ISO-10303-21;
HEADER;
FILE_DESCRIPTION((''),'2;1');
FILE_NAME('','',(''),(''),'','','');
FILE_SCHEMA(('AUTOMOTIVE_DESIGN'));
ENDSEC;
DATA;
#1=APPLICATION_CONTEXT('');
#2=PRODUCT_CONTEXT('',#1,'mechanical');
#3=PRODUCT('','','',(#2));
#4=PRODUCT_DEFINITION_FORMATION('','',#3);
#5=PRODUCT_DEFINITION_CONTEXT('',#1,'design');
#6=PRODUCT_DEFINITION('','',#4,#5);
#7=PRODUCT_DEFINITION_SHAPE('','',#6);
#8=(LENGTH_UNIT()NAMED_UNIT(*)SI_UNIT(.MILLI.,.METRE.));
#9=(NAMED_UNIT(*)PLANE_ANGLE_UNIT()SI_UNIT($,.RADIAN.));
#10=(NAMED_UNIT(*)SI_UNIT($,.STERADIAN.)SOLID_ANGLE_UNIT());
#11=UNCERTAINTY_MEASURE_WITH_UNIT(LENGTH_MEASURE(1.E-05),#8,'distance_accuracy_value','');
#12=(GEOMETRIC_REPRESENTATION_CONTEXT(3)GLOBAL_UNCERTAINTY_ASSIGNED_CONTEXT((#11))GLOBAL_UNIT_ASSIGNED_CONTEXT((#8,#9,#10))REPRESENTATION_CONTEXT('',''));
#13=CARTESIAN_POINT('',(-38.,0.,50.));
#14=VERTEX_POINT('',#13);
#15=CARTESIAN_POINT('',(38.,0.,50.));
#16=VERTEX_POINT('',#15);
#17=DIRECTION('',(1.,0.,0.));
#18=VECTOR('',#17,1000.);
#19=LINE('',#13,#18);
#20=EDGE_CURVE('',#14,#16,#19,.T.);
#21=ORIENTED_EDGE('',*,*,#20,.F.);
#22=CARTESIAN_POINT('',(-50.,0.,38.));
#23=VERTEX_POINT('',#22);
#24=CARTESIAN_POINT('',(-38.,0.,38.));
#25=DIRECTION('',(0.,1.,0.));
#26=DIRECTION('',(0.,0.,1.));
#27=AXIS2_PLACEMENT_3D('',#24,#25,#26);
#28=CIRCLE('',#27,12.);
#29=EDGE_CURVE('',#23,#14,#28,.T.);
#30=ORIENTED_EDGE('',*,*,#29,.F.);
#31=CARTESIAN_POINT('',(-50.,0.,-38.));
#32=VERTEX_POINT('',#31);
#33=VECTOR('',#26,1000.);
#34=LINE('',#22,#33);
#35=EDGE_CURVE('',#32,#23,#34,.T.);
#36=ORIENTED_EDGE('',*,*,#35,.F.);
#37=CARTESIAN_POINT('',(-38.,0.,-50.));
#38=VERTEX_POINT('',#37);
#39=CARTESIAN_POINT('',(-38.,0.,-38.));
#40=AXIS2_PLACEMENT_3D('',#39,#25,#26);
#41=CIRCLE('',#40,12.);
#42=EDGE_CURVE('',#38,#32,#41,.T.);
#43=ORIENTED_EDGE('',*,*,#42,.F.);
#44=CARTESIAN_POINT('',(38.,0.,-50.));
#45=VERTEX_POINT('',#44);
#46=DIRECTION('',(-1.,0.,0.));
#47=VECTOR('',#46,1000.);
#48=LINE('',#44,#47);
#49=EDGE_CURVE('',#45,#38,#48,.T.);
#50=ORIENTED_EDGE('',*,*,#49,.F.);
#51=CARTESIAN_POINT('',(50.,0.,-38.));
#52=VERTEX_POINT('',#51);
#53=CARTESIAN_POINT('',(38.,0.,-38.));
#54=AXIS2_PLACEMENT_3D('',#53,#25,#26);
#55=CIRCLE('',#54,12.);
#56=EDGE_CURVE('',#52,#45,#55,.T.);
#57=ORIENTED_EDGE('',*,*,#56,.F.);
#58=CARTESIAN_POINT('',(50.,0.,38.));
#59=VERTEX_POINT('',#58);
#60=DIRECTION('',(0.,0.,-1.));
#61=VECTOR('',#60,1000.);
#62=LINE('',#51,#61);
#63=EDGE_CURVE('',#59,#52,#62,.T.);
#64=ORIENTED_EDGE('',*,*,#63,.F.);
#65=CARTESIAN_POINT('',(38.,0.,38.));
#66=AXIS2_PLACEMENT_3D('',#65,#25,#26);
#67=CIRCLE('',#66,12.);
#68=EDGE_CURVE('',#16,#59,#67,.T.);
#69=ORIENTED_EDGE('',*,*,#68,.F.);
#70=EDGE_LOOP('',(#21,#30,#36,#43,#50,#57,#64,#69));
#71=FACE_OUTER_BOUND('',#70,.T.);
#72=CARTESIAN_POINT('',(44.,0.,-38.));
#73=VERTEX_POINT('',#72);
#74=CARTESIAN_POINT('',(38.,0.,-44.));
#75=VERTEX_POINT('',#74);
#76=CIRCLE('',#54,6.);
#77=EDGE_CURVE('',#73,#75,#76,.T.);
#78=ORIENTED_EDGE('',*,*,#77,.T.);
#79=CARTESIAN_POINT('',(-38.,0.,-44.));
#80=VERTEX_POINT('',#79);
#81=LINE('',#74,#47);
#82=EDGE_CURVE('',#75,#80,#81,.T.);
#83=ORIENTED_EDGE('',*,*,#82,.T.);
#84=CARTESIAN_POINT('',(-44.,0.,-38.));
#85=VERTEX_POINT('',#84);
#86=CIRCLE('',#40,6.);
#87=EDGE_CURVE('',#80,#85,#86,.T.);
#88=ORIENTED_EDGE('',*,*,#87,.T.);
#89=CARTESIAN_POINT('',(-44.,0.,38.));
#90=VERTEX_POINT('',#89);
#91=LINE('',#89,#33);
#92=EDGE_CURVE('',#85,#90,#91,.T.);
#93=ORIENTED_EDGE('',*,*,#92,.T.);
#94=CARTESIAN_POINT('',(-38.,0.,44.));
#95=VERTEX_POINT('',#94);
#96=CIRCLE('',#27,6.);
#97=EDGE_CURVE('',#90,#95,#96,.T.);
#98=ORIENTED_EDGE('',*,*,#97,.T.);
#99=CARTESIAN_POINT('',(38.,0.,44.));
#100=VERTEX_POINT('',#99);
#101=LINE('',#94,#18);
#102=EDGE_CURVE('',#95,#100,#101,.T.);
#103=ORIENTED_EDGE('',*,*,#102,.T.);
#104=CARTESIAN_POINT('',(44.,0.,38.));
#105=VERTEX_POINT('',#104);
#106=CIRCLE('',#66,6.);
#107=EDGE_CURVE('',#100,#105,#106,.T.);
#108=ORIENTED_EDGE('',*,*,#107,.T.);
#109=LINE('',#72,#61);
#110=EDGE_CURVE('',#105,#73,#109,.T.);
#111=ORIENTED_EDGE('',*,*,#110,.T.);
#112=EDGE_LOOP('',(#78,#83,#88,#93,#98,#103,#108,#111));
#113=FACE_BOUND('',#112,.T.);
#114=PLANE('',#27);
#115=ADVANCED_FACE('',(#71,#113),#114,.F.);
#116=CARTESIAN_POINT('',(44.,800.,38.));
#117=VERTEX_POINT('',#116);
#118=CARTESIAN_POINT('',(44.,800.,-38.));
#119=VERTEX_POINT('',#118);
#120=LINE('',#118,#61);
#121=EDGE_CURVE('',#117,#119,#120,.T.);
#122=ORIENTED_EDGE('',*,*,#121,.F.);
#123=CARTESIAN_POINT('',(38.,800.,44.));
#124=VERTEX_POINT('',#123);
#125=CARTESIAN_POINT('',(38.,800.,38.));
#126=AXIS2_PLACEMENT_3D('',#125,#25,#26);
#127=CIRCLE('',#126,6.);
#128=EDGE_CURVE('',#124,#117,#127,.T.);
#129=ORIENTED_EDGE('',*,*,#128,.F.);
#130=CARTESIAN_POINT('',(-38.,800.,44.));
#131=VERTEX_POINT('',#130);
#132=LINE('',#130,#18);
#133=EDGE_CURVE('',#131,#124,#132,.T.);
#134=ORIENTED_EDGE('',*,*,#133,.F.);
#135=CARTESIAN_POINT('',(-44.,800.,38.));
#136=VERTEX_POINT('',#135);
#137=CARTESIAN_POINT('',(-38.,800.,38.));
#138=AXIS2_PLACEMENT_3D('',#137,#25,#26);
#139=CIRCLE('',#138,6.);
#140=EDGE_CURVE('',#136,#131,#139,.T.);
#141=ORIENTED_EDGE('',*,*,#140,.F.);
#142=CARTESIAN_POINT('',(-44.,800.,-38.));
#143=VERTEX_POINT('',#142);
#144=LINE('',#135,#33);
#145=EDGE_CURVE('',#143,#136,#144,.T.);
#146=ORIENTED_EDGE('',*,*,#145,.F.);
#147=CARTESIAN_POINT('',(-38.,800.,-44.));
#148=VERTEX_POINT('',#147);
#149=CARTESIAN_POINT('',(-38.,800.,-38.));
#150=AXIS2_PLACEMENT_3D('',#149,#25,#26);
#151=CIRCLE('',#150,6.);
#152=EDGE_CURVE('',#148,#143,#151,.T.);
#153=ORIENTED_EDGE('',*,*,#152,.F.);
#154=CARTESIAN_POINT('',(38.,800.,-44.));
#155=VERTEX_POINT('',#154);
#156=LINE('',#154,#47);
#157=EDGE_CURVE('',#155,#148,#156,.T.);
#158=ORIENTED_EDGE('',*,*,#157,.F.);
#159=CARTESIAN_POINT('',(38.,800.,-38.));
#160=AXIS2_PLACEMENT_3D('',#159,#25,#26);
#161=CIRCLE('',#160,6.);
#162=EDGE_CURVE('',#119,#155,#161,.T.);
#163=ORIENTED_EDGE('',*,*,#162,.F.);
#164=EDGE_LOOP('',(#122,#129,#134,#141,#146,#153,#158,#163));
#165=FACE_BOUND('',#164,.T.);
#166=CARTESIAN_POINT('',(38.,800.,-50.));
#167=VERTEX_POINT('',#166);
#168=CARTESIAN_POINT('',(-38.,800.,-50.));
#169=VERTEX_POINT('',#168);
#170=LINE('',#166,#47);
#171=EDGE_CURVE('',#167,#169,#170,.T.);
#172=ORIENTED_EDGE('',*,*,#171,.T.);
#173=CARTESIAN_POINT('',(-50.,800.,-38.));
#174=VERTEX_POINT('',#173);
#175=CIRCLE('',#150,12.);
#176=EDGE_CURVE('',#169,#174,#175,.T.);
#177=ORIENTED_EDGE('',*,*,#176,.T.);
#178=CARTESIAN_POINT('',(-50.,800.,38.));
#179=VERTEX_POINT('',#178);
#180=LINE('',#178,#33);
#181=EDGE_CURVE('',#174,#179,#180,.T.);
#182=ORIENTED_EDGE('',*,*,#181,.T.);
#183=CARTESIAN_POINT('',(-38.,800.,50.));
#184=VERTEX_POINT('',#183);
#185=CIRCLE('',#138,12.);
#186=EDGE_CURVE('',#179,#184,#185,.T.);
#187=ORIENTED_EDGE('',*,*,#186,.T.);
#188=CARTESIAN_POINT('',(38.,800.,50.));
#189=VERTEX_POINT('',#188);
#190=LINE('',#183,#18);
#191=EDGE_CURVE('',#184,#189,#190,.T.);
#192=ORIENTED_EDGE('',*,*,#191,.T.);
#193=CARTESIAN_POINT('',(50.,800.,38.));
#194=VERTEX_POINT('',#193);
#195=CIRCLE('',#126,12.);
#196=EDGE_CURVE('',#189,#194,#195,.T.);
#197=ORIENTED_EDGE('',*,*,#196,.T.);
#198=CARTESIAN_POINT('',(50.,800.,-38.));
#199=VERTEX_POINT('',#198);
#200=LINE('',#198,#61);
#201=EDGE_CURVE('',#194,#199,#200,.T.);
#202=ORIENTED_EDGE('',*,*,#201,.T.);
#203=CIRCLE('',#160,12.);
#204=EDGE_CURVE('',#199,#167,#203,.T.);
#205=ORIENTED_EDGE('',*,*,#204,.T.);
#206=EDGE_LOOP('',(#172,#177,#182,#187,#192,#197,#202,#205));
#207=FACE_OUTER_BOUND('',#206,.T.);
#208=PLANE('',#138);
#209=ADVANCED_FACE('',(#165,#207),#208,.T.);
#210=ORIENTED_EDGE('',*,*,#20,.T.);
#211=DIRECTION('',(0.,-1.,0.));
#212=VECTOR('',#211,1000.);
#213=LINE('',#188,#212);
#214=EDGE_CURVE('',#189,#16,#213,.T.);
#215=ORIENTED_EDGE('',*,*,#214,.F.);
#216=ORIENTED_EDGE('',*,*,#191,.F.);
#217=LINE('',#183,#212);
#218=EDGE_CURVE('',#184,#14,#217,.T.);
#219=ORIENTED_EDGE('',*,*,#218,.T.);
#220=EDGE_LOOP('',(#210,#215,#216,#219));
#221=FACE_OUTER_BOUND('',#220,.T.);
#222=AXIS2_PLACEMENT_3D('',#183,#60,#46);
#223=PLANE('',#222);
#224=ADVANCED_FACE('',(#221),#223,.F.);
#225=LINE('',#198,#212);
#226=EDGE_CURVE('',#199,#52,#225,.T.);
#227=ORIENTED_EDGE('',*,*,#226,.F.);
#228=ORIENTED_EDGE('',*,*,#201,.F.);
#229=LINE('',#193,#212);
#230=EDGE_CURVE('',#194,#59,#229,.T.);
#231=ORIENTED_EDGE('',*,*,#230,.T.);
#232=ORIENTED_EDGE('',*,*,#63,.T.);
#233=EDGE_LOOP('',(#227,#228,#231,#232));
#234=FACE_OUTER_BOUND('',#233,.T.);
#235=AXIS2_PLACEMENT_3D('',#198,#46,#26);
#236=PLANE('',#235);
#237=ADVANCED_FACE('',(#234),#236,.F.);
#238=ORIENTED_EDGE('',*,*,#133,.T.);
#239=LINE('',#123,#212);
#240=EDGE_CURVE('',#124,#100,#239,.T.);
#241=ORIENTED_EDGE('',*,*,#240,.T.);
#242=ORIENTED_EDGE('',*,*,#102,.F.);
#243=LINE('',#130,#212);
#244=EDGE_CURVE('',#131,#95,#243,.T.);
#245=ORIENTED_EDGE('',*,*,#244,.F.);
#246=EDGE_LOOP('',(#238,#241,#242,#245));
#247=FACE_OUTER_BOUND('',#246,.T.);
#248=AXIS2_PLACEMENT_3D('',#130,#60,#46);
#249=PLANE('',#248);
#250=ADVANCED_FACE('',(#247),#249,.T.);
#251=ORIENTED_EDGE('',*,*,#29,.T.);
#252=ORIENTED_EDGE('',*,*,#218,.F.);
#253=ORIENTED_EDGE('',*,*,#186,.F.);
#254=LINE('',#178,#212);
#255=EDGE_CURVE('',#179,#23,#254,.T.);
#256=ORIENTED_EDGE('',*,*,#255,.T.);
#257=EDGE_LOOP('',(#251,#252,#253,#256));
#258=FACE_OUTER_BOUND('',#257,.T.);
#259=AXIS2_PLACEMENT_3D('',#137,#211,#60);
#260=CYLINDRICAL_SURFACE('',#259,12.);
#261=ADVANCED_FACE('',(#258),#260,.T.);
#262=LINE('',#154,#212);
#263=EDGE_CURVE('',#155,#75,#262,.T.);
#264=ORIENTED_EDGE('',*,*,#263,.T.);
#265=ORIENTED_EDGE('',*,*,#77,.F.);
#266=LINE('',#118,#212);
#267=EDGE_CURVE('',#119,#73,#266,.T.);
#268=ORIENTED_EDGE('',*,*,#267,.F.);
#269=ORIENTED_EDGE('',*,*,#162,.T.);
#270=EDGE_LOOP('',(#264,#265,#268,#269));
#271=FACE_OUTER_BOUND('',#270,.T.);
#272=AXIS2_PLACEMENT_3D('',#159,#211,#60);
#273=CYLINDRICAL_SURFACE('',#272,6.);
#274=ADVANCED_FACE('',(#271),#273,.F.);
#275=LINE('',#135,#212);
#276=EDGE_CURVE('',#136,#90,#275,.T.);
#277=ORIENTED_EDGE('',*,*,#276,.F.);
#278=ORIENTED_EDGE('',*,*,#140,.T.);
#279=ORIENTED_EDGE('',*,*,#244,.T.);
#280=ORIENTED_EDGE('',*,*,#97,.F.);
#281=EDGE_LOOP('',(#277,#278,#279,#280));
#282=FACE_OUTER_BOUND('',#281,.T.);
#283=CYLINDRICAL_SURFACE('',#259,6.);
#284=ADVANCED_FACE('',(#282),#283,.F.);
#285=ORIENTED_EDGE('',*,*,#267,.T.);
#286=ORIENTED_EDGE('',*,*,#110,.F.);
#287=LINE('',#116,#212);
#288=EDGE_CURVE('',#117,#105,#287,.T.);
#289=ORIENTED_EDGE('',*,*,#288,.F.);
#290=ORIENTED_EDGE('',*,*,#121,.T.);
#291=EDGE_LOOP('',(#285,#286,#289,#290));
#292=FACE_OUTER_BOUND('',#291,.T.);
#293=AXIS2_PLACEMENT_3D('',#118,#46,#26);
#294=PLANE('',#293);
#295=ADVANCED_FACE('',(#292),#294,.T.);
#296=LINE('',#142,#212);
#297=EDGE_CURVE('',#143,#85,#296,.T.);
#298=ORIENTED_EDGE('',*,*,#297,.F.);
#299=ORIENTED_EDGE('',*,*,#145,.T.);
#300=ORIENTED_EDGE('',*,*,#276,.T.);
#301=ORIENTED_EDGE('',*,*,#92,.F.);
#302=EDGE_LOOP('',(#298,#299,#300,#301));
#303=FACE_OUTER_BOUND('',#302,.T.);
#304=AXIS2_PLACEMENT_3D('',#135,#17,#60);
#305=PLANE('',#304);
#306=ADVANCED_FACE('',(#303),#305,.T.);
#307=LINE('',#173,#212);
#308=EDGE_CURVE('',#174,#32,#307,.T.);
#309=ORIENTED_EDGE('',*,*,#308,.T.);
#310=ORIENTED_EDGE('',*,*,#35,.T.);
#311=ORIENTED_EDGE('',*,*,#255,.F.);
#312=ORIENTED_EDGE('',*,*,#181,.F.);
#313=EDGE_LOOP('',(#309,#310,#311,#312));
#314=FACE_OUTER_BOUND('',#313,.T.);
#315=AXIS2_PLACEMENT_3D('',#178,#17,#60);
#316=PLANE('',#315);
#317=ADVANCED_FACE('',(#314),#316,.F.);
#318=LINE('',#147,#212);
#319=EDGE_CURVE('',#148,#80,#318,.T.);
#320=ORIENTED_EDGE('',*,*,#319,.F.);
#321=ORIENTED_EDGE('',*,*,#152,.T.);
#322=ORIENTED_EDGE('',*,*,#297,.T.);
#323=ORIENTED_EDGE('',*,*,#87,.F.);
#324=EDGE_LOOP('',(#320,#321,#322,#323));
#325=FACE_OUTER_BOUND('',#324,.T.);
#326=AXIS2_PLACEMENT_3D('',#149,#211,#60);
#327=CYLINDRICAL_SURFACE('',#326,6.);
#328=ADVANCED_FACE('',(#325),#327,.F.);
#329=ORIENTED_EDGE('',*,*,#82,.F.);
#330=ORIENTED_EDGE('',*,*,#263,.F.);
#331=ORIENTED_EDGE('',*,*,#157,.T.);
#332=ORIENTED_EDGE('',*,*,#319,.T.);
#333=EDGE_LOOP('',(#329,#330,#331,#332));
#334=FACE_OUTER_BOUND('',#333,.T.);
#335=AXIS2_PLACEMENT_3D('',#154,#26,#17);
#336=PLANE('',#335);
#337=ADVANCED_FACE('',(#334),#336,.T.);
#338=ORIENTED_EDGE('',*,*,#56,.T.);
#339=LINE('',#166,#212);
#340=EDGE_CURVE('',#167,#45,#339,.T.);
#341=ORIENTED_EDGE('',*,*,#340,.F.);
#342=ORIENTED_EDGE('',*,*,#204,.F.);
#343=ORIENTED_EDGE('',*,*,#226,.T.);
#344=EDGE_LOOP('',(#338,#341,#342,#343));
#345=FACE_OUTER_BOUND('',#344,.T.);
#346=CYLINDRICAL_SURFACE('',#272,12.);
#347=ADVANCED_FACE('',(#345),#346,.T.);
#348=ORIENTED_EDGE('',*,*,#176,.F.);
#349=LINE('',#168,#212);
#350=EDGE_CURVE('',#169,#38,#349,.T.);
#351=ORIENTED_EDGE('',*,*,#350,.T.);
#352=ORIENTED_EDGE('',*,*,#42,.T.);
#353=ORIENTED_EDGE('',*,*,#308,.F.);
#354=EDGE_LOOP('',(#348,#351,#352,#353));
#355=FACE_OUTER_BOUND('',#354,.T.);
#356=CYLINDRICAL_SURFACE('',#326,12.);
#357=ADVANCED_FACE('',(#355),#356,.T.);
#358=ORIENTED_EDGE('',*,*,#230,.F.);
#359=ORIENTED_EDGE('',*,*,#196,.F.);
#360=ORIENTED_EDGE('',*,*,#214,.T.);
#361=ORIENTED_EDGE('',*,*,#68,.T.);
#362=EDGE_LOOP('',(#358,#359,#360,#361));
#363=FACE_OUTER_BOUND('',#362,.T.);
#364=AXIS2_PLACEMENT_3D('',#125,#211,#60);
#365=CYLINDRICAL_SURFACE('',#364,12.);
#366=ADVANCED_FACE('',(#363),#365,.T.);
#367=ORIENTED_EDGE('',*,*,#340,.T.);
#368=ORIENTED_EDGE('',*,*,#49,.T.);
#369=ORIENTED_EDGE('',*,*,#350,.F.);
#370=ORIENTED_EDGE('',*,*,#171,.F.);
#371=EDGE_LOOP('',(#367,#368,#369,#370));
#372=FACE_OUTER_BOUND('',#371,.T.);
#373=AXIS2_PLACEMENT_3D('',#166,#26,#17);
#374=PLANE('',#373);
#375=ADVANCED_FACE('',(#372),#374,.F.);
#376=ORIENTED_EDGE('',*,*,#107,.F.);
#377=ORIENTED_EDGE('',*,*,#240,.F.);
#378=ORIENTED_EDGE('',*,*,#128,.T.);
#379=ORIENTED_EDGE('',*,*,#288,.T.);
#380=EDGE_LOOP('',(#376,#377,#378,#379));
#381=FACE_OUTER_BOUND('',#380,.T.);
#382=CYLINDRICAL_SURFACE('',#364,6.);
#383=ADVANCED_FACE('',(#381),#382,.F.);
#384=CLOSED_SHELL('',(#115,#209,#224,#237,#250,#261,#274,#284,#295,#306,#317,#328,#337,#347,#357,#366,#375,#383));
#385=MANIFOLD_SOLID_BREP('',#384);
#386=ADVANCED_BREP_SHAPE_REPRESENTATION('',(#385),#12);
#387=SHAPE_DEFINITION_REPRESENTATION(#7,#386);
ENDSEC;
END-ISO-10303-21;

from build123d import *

# Parameters (mm, degrees)
GB_T_6728_2002_SQUARE_HOLLOW_SECTION_100_DEPTH = 800


with BuildPart() as part:
    # Sketch11 → GB/T 6728-2002 square hollow section 100×100×6(1) (new body)
    with BuildSketch(Plane(origin=(0, 0, 0), x_dir=(-1, 0, 0), z_dir=(0, 1, 0))):
        with BuildLine():
            Line((-38, -50), (38, -50))
            ThreePointArc((38, -50), (46.485281374, -46.485281374), (50, -38))
            Line((50, -38), (50, 38))
            ThreePointArc((50, 38), (46.485281374, 46.485281374), (38, 50))
            Line((38, 50), (-38, 50))
            ThreePointArc((-38, 50), (-46.485281374, 46.485281374), (-50, 38))
            Line((-50, 38), (-50, -38))
            ThreePointArc((-50, -38), (-46.485281374, -46.485281374), (-38, -50))
        make_face()
        with BuildLine():
            Line((-38, -44), (38, -44))
            ThreePointArc((38, -44), (42.242640687, -42.242640687), (44, -38))
            Line((44, -38), (44, 38))
            ThreePointArc((44, 38), (42.242640687, 42.242640687), (38, 44))
            Line((38, 44), (-38, 44))
            ThreePointArc((-38, 44), (-42.242640687, 42.242640687), (-44, 38))
            Line((-44, 38), (-44, -38))
            ThreePointArc((-44, -38), (-42.242640687, -42.242640687), (-38, -44))
        make_face(mode=Mode.SUBTRACT)
    extrude(amount=GB_T_6728_2002_SQUARE_HOLLOW_SECTION_100_DEPTH)


solid = part.part
